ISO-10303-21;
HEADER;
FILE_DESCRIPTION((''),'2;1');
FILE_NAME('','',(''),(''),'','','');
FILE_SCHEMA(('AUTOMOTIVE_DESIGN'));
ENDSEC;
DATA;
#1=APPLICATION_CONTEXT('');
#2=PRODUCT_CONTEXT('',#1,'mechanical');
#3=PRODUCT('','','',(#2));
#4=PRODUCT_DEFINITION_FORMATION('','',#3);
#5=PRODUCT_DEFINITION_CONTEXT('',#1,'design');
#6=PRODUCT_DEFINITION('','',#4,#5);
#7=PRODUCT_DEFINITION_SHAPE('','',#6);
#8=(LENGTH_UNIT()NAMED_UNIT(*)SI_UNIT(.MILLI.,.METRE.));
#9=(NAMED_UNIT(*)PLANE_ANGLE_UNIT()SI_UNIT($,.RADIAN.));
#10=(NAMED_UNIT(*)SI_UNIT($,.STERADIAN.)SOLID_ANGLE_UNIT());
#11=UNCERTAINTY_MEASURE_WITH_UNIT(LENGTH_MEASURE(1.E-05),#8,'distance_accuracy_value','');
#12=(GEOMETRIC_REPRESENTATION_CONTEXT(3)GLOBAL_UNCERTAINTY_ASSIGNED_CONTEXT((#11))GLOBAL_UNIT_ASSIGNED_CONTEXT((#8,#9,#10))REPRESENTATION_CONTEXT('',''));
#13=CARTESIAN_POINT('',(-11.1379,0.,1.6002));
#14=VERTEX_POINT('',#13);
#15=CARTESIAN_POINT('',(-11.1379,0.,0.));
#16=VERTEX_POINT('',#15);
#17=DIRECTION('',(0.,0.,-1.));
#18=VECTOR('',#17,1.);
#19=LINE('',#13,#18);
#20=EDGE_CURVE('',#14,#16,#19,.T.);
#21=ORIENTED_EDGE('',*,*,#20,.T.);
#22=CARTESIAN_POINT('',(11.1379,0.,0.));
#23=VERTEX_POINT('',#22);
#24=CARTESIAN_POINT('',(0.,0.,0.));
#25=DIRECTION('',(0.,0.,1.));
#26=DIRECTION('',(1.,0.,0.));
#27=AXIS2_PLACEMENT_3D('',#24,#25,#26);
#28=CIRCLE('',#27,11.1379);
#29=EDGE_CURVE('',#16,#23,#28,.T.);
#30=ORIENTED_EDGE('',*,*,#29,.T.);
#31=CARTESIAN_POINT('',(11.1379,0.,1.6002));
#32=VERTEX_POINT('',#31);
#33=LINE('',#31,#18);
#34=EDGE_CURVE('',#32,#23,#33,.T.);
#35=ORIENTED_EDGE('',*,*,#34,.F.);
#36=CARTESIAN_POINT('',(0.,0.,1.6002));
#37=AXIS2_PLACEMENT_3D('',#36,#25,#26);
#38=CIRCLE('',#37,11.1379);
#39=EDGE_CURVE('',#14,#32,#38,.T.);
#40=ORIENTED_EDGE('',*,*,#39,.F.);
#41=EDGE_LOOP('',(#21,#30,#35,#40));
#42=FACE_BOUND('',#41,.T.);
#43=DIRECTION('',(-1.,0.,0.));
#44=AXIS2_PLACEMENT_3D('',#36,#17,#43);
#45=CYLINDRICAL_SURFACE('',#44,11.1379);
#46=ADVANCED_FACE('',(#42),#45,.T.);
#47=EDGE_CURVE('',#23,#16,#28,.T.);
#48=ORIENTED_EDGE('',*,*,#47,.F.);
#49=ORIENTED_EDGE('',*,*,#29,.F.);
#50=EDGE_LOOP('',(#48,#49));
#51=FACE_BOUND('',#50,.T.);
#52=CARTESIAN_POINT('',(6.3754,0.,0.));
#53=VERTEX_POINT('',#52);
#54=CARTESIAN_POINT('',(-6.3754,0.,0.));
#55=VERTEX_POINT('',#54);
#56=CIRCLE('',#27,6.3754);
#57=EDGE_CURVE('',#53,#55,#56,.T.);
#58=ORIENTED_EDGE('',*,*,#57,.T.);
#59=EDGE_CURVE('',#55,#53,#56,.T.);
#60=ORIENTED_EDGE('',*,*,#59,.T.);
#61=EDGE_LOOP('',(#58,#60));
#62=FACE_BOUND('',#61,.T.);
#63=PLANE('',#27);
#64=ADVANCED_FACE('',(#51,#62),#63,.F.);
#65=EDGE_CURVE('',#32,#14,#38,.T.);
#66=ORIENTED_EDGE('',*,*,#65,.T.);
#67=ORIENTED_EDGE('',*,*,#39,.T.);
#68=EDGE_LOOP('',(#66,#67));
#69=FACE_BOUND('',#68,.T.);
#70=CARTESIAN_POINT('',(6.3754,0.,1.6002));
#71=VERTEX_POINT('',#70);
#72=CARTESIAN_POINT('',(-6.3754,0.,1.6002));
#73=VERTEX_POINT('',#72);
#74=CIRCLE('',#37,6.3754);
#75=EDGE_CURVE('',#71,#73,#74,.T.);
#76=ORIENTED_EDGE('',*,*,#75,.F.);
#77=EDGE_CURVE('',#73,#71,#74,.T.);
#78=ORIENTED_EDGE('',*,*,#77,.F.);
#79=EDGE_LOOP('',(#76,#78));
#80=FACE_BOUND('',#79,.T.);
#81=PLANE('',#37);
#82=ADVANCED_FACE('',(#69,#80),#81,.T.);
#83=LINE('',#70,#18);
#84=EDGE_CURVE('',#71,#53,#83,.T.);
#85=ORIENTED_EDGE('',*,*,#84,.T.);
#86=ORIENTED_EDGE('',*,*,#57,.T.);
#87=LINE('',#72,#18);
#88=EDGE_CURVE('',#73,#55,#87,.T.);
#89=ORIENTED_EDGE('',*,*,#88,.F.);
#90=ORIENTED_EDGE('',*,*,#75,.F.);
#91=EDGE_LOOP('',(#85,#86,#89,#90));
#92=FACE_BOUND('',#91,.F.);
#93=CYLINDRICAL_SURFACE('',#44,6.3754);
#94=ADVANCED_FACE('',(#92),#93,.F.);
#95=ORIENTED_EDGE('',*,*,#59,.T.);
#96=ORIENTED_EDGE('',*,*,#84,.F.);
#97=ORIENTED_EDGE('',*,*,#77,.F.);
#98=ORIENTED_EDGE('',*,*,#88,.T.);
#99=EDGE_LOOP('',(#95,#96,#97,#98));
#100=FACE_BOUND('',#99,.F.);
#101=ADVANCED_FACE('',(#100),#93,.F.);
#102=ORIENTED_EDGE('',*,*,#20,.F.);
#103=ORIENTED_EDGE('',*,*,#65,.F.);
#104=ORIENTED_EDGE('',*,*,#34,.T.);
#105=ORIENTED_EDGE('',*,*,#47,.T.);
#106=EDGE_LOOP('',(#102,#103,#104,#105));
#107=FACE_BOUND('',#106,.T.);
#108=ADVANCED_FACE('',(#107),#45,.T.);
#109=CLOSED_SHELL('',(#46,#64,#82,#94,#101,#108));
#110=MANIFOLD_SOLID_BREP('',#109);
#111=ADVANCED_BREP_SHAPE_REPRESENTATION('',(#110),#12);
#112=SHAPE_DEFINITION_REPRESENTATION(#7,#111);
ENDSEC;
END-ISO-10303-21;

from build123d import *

# Parameters (mm, degrees)
SKETCH1_R           = 11.1379
SKETCH1_R_2         = 6.3754
BOSS_EXTRUDE1_DEPTH = 1.6002


with BuildPart() as part:
    # Sketch1 → Boss-Extrude1 (new body)
    with BuildSketch(Plane.XY):
        Circle(SKETCH1_R)
        Circle(SKETCH1_R_2, mode=Mode.SUBTRACT)
    extrude(amount=BOSS_EXTRUDE1_DEPTH)


solid = part.part
